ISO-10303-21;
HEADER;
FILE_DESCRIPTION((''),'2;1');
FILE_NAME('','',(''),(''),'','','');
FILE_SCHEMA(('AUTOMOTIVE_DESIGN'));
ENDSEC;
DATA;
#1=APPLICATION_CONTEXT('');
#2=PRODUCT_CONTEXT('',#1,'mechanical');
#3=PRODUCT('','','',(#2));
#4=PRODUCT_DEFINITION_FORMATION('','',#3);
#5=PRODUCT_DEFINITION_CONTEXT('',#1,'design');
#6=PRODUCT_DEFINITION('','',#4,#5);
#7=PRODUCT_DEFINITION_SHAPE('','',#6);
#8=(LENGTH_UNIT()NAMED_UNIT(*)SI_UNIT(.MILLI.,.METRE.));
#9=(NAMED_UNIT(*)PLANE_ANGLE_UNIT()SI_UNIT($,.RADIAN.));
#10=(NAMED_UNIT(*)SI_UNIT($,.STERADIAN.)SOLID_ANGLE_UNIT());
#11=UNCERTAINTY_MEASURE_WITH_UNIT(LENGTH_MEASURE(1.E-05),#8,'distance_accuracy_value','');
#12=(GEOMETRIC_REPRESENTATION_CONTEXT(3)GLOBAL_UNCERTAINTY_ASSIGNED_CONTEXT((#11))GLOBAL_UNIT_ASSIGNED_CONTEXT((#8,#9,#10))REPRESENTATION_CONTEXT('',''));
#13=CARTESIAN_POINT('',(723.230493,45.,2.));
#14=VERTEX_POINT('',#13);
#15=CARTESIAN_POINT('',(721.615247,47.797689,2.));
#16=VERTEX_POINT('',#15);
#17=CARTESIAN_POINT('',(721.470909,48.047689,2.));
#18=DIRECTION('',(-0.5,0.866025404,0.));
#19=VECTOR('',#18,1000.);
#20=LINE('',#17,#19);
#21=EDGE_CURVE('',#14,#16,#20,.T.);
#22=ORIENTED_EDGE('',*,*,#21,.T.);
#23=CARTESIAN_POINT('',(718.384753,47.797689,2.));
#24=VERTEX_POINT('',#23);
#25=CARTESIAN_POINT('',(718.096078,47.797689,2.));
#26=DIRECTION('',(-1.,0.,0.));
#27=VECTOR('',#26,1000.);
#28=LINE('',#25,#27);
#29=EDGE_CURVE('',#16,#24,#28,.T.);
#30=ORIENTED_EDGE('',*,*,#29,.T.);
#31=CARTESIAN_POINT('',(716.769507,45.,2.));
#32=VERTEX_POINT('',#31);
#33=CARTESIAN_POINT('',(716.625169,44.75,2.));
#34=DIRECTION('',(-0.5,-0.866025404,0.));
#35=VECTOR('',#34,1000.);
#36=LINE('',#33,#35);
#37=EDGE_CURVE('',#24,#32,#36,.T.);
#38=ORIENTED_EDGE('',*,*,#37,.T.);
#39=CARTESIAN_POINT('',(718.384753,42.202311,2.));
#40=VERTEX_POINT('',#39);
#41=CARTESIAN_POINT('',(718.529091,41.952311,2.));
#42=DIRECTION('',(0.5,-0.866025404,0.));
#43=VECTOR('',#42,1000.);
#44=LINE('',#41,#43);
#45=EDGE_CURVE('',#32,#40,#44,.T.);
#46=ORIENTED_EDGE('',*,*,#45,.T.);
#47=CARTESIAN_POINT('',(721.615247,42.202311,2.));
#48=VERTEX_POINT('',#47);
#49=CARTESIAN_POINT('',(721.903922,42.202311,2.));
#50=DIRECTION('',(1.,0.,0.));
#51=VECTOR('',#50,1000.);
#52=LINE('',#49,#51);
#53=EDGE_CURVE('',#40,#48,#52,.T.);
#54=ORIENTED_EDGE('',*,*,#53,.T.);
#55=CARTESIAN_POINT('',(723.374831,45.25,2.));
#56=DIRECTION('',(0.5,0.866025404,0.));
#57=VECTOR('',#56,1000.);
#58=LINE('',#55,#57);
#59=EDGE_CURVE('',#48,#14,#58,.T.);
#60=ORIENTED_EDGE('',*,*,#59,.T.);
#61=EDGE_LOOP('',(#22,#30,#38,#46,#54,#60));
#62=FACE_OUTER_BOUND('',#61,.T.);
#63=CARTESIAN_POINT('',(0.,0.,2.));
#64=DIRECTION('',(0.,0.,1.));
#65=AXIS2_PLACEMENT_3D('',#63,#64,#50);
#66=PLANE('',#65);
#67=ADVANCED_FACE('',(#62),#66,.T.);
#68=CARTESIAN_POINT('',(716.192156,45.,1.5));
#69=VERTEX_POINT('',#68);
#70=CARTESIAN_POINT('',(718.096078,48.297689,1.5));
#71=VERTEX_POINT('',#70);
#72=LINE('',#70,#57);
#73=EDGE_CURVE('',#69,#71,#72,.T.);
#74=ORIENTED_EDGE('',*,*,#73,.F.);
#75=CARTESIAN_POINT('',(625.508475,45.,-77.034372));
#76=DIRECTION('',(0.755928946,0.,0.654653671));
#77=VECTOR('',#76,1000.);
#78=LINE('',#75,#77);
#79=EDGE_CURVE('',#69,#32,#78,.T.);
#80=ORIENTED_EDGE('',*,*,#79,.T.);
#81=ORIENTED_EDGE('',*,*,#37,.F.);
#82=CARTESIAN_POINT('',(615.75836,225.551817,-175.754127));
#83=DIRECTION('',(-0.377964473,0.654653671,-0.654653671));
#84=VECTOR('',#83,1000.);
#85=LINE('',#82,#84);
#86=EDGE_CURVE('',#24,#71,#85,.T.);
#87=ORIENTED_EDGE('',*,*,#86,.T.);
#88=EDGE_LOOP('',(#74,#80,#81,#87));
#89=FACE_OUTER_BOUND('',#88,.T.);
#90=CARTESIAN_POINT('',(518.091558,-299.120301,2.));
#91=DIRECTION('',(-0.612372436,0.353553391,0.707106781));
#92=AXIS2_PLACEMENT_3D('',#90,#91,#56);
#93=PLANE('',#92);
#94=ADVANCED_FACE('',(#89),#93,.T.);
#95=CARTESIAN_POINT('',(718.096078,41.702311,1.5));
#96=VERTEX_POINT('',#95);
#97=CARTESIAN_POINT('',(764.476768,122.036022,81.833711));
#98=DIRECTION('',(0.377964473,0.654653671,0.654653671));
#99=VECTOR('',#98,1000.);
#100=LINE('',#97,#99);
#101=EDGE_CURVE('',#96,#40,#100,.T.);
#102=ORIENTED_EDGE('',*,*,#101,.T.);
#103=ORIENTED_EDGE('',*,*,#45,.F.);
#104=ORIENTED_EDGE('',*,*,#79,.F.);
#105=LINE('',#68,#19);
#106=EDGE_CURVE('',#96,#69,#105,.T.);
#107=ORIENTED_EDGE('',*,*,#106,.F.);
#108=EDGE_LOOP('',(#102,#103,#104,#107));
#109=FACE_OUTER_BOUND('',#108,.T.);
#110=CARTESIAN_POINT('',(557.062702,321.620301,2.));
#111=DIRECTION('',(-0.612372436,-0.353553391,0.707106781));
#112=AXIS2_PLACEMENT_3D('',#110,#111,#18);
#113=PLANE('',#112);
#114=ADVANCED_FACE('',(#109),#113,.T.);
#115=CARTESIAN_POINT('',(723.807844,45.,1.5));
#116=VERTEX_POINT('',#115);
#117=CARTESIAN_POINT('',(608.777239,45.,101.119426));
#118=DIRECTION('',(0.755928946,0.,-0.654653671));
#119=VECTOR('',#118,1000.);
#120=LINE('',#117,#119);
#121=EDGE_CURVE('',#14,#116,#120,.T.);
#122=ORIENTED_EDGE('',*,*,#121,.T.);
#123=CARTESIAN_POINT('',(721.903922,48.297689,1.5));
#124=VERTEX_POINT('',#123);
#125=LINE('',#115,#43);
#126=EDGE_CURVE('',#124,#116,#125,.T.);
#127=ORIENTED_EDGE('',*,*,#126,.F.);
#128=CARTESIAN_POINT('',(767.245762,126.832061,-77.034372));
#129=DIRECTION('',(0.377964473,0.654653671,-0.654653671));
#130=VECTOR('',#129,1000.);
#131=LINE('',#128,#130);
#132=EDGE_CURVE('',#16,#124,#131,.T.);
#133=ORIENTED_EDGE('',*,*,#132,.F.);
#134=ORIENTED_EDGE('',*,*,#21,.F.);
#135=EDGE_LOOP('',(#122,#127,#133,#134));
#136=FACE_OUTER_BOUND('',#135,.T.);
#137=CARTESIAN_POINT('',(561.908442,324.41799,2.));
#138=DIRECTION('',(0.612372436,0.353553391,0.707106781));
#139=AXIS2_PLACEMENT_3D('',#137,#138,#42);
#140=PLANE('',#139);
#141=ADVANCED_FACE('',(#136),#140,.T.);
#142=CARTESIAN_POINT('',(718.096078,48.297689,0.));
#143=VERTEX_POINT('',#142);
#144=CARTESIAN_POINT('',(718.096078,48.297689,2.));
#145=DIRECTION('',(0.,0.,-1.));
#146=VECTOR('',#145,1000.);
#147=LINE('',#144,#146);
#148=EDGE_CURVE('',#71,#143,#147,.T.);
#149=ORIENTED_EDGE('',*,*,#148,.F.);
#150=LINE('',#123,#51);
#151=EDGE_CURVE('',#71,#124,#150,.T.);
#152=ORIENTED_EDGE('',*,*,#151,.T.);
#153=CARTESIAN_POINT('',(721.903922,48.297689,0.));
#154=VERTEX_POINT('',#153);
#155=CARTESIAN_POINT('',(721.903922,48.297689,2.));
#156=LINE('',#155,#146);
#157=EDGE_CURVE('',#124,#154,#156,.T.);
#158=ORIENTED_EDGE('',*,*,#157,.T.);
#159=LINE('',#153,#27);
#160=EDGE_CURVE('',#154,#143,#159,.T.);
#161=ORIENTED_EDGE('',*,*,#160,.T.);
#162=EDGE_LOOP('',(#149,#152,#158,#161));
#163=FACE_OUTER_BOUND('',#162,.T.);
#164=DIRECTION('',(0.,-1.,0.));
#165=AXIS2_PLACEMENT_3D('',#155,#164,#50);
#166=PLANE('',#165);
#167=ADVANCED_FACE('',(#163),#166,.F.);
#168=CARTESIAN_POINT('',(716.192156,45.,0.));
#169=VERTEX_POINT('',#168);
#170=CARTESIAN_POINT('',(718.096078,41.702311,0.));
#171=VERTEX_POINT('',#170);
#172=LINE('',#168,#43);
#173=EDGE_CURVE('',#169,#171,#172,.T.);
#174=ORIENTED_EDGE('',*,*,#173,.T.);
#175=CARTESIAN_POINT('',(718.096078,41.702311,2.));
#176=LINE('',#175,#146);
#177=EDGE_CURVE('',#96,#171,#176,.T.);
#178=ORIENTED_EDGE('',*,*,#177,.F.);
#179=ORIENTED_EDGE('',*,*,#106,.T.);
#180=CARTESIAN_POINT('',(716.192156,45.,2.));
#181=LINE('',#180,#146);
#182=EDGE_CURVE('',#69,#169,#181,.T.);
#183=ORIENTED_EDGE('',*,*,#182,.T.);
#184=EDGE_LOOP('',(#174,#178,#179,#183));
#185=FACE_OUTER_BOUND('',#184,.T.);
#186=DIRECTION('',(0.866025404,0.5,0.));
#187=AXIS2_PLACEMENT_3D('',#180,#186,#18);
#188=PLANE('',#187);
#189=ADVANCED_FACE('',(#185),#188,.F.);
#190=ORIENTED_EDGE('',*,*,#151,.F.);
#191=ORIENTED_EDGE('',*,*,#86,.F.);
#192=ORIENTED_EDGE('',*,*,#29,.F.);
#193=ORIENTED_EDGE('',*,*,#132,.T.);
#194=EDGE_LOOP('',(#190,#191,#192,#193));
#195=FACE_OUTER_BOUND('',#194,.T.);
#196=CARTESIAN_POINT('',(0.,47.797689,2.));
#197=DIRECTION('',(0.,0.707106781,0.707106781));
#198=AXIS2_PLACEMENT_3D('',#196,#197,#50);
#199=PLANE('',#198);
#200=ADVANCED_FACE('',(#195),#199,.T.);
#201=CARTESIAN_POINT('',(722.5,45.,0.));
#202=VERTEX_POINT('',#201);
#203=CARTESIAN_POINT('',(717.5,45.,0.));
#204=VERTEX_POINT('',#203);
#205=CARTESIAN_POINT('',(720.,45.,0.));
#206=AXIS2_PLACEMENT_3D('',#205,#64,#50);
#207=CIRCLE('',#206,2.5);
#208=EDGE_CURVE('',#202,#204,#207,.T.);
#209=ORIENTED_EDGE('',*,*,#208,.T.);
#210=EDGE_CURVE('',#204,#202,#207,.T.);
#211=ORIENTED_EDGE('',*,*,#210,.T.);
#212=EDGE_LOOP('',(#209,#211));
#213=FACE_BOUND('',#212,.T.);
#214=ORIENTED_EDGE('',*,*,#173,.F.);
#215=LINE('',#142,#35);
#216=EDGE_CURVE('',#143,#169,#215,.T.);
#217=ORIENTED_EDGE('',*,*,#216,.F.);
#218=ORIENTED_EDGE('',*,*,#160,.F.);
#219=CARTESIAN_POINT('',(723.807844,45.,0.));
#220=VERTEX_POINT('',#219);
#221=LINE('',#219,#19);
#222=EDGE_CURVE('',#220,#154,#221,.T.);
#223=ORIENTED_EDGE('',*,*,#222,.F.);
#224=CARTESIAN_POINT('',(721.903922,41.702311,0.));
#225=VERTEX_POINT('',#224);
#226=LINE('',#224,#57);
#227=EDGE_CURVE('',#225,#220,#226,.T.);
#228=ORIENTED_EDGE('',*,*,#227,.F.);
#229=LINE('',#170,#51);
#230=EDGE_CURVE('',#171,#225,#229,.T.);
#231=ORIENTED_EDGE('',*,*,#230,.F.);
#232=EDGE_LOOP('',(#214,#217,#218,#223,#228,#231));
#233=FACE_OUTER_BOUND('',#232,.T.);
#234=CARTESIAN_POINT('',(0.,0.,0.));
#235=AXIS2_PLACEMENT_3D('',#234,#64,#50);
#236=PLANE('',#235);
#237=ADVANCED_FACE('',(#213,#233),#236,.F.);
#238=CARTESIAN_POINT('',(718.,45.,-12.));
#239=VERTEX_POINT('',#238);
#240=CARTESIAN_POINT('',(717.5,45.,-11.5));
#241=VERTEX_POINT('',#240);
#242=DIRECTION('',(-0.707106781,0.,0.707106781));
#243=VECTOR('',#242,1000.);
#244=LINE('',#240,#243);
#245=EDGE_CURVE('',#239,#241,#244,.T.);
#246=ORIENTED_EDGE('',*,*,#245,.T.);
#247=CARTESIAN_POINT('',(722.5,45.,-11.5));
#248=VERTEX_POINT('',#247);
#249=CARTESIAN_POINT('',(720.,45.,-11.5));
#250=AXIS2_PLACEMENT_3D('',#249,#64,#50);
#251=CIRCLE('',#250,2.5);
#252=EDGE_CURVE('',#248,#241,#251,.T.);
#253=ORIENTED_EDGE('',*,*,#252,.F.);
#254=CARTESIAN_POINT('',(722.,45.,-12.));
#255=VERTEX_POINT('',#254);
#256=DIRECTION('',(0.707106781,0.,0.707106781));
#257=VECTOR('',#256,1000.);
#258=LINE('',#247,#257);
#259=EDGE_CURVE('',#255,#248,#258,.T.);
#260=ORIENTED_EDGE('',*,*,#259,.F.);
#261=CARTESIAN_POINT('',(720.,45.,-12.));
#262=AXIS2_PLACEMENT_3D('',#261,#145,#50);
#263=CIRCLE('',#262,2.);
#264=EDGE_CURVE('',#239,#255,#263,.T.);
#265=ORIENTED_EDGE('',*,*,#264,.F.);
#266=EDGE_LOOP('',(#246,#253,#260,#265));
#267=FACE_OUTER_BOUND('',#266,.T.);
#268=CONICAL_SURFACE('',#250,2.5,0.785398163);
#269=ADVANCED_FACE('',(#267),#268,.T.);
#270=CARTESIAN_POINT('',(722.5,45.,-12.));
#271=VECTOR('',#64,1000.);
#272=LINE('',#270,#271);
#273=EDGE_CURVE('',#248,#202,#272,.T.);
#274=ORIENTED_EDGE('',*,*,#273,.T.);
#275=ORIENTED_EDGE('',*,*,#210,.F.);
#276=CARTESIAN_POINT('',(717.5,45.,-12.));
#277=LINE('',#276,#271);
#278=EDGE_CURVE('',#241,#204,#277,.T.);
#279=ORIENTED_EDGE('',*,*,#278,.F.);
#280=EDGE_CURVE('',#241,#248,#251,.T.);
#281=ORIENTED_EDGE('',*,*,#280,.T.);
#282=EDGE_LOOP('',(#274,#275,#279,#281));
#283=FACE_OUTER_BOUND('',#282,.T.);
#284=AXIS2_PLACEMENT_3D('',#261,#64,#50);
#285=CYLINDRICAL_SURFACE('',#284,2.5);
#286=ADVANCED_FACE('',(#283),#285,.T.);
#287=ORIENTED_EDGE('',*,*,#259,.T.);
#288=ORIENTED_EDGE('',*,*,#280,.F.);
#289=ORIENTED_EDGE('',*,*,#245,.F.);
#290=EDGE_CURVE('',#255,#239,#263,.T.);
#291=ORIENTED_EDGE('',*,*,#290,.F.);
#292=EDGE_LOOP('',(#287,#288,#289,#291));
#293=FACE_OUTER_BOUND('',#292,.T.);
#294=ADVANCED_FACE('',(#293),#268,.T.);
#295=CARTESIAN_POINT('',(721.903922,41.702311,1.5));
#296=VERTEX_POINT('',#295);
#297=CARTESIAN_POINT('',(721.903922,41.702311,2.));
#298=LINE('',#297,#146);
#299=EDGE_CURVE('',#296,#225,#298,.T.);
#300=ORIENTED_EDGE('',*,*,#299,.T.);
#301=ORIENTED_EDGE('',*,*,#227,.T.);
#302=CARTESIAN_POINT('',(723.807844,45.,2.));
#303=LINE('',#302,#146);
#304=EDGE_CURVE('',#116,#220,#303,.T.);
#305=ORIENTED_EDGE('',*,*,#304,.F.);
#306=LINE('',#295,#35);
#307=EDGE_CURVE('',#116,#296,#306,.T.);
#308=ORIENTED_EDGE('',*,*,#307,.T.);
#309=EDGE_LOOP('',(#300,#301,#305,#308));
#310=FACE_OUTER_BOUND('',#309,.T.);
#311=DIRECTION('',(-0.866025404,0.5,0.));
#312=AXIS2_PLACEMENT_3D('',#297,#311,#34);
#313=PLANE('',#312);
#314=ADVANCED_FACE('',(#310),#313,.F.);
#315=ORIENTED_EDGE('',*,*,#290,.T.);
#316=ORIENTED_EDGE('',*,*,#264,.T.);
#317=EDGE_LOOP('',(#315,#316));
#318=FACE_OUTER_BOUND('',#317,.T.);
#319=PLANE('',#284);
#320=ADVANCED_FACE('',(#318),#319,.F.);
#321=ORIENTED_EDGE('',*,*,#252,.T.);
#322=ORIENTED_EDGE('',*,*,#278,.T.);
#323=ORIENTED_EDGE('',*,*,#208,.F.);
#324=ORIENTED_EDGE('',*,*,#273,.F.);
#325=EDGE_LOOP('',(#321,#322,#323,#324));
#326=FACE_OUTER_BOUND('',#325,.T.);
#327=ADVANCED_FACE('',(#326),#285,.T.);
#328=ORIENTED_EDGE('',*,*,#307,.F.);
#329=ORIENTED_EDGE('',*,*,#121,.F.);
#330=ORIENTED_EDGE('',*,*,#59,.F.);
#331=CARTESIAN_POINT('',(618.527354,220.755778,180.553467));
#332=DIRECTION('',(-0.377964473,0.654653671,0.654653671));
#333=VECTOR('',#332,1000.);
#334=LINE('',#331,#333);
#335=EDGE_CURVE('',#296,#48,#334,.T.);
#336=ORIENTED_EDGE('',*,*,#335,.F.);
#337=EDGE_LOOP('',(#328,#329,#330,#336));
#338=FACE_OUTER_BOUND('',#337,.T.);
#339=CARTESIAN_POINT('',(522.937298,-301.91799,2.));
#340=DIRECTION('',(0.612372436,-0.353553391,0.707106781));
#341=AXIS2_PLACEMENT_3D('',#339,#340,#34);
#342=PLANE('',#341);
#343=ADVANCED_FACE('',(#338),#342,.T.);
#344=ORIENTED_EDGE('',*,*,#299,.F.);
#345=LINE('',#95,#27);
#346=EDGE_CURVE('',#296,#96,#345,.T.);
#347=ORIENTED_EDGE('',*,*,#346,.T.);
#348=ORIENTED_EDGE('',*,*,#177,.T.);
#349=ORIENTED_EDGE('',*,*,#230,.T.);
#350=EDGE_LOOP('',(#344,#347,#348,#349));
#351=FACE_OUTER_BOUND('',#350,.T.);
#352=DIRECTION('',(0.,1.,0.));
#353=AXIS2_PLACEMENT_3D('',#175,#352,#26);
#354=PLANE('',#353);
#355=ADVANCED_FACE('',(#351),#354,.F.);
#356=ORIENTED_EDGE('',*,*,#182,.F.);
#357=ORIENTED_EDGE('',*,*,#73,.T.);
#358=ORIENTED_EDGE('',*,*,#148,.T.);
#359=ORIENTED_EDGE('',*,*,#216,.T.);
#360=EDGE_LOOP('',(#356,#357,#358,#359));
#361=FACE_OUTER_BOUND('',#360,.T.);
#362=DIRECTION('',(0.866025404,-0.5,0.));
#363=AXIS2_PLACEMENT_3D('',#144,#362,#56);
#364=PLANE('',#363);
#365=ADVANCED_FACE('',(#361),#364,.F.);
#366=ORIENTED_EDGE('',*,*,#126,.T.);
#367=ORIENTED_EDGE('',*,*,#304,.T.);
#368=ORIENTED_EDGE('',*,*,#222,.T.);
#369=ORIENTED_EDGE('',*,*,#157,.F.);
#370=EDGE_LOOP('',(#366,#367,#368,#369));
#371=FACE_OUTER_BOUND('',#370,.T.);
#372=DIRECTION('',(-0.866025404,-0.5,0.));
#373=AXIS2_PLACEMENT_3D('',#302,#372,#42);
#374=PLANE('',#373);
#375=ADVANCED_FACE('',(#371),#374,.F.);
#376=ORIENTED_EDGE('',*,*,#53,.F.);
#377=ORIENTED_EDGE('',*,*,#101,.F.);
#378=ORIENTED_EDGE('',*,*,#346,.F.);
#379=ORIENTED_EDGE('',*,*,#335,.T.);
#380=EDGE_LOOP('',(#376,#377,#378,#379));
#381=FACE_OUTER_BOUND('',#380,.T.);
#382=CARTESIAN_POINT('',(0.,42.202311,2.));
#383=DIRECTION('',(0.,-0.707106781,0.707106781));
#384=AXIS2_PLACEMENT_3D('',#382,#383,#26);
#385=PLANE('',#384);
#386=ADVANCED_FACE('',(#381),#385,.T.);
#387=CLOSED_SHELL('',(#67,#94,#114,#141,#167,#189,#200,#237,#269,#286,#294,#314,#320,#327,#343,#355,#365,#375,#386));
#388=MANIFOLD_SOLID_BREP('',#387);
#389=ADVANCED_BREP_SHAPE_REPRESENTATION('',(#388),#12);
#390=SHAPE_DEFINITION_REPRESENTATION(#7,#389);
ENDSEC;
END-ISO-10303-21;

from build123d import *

# Parameters (mm, degrees)
SKETCH1_R           = 2.5
BOSS_EXTRUDE1_DEPTH = 12
BOSS_EXTRUDE2_DEPTH = 2
CHAMFER1_SIZE       = 0.5


with BuildPart() as part:
    # Sketch1 → Boss-Extrude1 (new body)
    with BuildSketch(Plane.XY):
        with Locations((720, 45)):
            Circle(SKETCH1_R)
    extrude(amount=-BOSS_EXTRUDE1_DEPTH)

    # Sketch2 → Boss-Extrude2 (add)
    with BuildSketch(Plane.XY):
        Polygon((718.096078213, 41.702310731), (721.903921787, 41.702310731), (723.807843574, 45), (721.903921787, 48.297689269), (718.096078213, 48.297689269), (716.192156426, 45), align=None)
    extrude(amount=BOSS_EXTRUDE2_DEPTH)

    # Chamfer1
    chamfer1_edges = [part.edges().sort_by_distance(p)[0] for p in [
        (717.5, 45, -12),
        (717.144117319, 43.351155365, 2),
        (720, 41.702310731, 2),
        (722.855882681, 43.351155365, 2),
        (722.855882681, 46.648844635, 2),
        (720, 48.297689269, 2),
        (717.144117319, 46.648844635, 2),
    ]]
    chamfer(chamfer1_edges, length=CHAMFER1_SIZE)


solid = part.part
